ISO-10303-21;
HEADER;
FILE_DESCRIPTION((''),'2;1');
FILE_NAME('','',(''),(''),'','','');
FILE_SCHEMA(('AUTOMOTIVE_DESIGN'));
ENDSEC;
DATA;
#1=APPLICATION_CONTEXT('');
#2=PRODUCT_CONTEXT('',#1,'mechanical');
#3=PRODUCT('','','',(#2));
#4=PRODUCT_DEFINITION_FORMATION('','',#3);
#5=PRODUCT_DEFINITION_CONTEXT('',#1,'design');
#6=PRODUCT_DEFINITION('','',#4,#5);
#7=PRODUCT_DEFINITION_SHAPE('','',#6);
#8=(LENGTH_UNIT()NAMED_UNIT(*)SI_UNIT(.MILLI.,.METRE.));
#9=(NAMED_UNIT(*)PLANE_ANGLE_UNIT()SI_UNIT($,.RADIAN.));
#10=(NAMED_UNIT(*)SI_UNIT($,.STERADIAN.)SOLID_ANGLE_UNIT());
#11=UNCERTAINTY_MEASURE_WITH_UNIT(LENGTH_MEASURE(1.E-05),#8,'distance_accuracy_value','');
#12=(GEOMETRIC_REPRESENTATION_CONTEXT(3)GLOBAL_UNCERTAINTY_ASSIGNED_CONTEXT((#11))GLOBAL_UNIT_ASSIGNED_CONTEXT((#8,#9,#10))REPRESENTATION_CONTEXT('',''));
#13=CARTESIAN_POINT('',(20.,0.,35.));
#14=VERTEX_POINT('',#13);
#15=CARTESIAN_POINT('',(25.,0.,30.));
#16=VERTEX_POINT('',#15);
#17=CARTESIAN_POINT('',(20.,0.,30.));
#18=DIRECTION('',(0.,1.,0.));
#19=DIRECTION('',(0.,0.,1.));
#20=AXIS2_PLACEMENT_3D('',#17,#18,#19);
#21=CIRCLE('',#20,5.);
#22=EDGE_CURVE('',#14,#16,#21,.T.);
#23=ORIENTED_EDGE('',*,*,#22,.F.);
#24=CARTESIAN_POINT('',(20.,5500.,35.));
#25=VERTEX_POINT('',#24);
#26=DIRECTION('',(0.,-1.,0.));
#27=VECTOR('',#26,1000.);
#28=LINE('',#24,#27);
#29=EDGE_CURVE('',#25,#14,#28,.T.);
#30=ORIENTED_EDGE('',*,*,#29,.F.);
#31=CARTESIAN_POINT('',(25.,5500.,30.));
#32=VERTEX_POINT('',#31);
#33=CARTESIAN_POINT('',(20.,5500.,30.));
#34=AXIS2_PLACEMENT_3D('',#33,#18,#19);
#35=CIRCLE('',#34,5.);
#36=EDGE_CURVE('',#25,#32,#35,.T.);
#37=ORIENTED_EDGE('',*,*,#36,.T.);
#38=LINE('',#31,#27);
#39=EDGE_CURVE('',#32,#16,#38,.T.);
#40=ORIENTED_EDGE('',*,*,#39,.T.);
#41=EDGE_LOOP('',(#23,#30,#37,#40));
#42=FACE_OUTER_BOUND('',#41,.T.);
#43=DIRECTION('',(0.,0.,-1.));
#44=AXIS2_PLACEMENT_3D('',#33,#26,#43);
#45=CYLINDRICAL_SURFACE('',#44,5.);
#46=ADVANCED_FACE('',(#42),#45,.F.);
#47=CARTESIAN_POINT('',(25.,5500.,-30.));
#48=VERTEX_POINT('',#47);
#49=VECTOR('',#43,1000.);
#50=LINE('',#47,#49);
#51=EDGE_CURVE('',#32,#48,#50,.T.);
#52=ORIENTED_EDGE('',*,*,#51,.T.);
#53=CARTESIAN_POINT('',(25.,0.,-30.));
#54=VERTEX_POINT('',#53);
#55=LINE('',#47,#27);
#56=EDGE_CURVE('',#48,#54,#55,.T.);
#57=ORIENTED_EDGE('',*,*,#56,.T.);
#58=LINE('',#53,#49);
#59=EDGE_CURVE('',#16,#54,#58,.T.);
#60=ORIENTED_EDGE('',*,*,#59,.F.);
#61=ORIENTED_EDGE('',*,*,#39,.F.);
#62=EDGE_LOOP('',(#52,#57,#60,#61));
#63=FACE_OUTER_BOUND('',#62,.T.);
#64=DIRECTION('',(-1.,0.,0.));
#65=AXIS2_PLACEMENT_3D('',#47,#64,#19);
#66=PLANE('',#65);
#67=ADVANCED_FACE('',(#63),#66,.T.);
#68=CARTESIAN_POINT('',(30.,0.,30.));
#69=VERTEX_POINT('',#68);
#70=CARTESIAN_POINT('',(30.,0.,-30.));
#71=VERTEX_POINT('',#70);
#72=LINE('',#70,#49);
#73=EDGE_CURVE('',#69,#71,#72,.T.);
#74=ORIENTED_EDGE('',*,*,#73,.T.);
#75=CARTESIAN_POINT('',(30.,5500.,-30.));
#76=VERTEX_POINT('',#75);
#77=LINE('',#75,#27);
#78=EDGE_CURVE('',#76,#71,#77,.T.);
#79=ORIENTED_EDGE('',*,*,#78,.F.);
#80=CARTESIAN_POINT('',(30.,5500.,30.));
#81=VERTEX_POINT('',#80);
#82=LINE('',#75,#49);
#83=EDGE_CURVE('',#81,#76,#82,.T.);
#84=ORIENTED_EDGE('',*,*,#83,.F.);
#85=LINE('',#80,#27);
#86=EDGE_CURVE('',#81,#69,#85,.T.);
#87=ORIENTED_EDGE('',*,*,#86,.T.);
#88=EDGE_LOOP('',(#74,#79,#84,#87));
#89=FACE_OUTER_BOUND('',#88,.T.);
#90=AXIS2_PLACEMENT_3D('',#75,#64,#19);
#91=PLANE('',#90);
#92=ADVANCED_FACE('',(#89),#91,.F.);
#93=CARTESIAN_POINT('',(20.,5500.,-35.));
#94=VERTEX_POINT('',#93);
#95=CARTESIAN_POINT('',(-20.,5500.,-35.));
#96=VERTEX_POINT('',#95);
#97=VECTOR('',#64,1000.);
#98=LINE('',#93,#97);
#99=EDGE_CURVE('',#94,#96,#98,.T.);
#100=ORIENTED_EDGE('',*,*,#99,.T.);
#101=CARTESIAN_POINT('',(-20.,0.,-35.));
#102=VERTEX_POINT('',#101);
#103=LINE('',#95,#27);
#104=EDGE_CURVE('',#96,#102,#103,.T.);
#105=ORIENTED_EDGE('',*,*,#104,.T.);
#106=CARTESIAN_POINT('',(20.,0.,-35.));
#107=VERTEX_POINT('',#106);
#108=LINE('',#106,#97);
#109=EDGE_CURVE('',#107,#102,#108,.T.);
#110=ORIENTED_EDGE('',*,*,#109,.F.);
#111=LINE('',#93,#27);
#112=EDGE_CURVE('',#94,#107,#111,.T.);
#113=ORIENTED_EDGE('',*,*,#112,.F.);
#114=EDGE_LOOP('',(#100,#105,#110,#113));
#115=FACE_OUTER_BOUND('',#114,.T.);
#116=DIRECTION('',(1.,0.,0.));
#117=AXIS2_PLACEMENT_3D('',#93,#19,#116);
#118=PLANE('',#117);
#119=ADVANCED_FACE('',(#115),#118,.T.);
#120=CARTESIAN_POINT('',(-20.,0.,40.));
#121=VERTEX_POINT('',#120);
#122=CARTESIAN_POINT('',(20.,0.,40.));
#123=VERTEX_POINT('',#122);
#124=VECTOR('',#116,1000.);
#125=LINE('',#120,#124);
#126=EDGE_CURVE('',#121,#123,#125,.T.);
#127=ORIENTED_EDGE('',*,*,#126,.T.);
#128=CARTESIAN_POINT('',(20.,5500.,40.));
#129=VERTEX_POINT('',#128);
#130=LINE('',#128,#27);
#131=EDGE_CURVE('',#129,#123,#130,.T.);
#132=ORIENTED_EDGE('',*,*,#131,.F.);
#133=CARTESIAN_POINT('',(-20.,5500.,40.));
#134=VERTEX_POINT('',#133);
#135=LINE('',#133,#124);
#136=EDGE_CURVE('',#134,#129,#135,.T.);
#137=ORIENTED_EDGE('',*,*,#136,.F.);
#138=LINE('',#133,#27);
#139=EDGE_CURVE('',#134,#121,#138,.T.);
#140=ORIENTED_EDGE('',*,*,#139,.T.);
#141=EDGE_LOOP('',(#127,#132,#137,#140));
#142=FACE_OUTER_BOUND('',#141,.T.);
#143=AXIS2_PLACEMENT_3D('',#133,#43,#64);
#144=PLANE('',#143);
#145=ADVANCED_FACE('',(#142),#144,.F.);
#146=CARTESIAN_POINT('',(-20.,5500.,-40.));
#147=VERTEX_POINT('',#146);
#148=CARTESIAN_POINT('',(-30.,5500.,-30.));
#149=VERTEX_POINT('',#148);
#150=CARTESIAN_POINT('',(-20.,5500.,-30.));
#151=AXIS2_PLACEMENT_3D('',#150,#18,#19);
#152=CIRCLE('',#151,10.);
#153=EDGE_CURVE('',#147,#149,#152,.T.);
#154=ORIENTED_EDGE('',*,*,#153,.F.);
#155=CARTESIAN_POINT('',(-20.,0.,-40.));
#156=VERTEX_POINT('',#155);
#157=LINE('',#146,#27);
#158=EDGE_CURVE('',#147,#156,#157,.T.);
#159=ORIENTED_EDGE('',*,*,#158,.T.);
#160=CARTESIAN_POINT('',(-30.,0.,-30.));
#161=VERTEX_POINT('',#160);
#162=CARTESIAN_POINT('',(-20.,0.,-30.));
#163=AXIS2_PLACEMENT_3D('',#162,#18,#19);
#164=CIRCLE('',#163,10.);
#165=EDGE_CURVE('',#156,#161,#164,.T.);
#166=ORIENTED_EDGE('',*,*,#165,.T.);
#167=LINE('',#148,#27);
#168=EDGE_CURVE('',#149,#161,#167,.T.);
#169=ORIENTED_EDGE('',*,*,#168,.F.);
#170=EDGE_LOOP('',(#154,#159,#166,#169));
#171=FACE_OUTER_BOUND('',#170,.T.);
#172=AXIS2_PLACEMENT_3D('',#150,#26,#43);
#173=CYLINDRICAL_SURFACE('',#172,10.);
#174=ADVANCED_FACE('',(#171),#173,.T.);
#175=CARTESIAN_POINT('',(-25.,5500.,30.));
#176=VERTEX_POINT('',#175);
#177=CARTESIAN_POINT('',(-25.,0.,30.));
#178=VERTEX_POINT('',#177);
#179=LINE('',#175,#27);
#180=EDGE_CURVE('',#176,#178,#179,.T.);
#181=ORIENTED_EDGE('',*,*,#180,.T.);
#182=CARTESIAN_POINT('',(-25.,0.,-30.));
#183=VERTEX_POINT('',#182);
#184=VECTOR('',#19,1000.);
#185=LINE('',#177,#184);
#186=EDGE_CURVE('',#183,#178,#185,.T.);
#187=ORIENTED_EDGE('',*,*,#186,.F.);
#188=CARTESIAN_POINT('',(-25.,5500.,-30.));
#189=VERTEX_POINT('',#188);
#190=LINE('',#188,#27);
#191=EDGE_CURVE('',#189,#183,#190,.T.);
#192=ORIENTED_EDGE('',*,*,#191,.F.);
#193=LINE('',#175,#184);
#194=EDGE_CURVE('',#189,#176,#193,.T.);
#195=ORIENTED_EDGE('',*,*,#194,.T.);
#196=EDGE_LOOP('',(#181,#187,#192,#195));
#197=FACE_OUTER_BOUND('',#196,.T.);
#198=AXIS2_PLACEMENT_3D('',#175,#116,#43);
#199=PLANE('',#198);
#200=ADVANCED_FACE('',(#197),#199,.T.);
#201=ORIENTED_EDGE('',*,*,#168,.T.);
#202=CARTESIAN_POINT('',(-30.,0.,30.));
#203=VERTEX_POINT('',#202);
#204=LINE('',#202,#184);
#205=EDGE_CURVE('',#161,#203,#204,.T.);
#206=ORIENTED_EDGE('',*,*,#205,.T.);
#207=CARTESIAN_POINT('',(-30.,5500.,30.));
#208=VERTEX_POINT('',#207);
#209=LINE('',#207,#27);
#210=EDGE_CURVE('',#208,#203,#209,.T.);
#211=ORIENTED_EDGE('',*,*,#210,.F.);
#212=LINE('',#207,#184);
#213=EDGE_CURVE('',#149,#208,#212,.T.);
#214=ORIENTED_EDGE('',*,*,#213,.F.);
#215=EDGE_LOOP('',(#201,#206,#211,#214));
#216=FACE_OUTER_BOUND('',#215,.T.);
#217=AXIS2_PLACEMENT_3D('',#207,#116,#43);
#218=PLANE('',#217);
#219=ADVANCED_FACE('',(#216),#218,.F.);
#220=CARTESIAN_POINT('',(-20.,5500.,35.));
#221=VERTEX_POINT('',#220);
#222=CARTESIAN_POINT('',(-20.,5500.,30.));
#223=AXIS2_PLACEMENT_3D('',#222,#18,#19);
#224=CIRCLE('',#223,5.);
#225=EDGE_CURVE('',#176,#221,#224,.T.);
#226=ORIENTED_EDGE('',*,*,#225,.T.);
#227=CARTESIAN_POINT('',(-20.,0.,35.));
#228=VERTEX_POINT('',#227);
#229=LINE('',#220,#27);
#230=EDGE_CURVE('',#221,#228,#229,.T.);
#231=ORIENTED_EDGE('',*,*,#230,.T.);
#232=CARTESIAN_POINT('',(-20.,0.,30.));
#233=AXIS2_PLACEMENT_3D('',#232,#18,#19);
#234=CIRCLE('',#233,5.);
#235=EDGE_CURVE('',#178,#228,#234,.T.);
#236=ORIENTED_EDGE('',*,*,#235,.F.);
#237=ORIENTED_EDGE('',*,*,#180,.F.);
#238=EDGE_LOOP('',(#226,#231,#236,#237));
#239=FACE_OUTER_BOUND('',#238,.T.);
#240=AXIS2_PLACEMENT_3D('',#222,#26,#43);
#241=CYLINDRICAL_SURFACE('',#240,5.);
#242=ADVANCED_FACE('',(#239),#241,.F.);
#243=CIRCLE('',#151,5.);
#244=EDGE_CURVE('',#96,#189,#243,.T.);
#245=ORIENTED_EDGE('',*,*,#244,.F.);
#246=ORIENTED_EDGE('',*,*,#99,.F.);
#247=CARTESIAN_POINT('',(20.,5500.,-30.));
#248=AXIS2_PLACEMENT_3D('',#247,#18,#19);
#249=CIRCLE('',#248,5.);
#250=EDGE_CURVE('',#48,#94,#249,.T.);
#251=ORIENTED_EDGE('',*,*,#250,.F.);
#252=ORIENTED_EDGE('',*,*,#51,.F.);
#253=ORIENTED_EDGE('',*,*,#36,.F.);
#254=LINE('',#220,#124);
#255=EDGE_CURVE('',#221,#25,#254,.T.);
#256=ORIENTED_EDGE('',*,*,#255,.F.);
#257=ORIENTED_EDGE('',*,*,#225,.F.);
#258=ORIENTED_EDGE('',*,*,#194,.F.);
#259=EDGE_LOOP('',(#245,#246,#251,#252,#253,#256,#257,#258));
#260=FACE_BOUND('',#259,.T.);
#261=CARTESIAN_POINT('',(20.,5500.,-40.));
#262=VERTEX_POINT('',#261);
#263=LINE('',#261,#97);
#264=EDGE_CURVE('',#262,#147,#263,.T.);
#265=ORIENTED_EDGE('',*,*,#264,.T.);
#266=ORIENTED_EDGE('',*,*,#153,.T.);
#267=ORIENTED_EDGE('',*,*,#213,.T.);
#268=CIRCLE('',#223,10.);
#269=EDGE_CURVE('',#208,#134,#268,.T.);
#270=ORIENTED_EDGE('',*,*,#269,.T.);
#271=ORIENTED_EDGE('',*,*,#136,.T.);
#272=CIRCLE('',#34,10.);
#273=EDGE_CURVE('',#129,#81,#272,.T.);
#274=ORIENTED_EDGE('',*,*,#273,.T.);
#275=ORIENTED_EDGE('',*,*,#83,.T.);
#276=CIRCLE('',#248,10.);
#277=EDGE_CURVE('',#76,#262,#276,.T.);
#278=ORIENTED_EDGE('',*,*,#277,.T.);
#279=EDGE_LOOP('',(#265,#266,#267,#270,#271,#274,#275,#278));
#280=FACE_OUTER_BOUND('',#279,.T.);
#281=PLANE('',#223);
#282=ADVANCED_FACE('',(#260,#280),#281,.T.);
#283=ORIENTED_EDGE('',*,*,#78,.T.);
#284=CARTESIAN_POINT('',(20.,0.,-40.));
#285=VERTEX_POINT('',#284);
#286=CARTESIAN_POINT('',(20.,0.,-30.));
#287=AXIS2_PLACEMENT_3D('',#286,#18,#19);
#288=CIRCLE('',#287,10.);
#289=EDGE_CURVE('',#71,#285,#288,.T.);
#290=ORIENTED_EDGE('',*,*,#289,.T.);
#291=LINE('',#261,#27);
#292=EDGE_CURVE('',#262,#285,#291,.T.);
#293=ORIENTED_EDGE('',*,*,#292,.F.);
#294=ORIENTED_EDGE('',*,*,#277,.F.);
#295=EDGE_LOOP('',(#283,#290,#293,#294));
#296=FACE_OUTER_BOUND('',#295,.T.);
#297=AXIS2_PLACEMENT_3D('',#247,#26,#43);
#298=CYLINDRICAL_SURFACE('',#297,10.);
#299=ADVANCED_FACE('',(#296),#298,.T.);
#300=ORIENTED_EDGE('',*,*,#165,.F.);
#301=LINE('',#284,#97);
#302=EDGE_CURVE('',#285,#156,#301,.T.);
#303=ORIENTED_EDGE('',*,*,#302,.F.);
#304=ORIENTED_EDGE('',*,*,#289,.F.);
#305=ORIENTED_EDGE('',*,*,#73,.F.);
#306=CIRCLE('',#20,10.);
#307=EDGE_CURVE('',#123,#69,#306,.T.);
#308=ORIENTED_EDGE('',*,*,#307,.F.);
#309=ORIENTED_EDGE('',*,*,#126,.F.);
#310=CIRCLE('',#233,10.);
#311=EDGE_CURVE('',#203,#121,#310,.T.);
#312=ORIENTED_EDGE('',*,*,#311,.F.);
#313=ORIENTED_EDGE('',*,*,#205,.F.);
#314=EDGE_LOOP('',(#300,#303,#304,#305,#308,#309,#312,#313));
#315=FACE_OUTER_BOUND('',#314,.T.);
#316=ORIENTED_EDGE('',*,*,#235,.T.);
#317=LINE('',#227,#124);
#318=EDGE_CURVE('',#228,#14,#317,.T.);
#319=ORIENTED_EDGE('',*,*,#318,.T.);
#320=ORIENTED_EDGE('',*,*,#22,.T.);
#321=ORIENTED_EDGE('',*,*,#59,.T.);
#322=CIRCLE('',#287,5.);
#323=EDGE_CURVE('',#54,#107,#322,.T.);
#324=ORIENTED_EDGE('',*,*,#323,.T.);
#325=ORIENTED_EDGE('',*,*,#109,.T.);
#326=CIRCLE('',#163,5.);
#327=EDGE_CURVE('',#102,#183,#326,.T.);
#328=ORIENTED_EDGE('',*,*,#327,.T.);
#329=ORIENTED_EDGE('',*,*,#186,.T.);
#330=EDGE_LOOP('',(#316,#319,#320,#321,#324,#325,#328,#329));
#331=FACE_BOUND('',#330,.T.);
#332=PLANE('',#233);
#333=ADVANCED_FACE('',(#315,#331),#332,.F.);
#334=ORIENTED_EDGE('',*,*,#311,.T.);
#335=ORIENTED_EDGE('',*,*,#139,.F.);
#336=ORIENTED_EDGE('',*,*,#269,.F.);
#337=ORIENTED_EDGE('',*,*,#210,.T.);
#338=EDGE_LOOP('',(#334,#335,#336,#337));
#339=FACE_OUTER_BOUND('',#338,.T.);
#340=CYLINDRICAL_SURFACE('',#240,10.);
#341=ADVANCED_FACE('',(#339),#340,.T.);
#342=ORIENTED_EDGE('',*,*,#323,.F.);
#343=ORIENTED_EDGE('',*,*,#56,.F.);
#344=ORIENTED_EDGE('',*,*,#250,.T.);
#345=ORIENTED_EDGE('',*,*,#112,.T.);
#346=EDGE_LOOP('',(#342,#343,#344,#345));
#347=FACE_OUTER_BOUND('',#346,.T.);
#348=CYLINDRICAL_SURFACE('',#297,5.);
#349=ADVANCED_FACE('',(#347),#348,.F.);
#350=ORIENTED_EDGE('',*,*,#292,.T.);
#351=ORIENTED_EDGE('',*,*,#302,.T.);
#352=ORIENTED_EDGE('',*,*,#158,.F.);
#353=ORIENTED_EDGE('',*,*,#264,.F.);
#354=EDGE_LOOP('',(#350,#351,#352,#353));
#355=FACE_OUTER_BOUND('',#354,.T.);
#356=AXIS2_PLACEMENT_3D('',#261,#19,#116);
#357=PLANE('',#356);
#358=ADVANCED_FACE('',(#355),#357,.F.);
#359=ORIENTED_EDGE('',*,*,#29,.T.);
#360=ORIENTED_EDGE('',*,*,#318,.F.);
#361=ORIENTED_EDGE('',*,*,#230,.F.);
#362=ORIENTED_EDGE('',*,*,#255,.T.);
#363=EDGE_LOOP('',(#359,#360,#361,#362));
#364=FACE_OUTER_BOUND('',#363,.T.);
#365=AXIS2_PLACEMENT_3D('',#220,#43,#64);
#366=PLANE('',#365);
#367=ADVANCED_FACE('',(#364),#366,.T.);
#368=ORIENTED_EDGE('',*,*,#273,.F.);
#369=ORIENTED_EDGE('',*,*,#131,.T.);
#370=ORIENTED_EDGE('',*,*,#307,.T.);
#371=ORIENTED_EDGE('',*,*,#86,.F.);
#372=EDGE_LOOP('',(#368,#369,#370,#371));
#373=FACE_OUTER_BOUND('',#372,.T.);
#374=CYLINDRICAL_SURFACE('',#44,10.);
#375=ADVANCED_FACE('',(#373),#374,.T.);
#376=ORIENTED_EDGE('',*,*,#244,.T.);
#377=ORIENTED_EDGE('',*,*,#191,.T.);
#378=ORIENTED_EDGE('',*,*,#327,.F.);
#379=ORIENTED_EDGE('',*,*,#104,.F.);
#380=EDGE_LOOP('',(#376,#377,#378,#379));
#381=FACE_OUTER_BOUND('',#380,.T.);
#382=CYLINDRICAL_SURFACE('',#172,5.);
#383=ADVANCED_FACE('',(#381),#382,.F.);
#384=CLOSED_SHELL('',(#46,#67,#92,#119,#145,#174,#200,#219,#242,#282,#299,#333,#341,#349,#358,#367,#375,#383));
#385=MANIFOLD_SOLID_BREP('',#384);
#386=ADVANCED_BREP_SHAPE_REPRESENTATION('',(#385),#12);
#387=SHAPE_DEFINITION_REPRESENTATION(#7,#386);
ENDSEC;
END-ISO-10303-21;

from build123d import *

# Parameters (mm, degrees)
COLD_FORMED_HOLLOW_STRUCTURAL_RECTANGULA_DEPTH = 5500


with BuildPart() as part:
    # Sketch1 → Cold-formed Hollow Structural Rectangular Steel(gb t6728-2002) 80×60×5(1) (new body)
    with BuildSketch(Plane(origin=(0, 0, 0), x_dir=(-1, 0, 0), z_dir=(0, 1, 0))):
        with BuildLine():
            Line((-20, -40), (20, -40))
            ThreePointArc((20, -40), (27.071067812, -37.071067812), (30, -30))
            Line((30, -30), (30, 30))
            ThreePointArc((30, 30), (27.071067812, 37.071067812), (20, 40))
            Line((20, 40), (-20, 40))
            ThreePointArc((-20, 40), (-27.071067812, 37.071067812), (-30, 30))
            Line((-30, 30), (-30, -30))
            ThreePointArc((-30, -30), (-27.071067812, -37.071067812), (-20, -40))
        make_face()
        with BuildLine():
            Line((-20, -35), (20, -35))
            ThreePointArc((20, -35), (23.535533906, -33.535533906), (25, -30))
            Line((25, -30), (25, 30))
            ThreePointArc((25, 30), (23.535533906, 33.535533906), (20, 35))
            Line((20, 35), (-20, 35))
            ThreePointArc((-20, 35), (-23.535533906, 33.535533906), (-25, 30))
            Line((-25, 30), (-25, -30))
            ThreePointArc((-25, -30), (-23.535533906, -33.535533906), (-20, -35))
        make_face(mode=Mode.SUBTRACT)
    extrude(amount=COLD_FORMED_HOLLOW_STRUCTURAL_RECTANGULA_DEPTH)


solid = part.part
